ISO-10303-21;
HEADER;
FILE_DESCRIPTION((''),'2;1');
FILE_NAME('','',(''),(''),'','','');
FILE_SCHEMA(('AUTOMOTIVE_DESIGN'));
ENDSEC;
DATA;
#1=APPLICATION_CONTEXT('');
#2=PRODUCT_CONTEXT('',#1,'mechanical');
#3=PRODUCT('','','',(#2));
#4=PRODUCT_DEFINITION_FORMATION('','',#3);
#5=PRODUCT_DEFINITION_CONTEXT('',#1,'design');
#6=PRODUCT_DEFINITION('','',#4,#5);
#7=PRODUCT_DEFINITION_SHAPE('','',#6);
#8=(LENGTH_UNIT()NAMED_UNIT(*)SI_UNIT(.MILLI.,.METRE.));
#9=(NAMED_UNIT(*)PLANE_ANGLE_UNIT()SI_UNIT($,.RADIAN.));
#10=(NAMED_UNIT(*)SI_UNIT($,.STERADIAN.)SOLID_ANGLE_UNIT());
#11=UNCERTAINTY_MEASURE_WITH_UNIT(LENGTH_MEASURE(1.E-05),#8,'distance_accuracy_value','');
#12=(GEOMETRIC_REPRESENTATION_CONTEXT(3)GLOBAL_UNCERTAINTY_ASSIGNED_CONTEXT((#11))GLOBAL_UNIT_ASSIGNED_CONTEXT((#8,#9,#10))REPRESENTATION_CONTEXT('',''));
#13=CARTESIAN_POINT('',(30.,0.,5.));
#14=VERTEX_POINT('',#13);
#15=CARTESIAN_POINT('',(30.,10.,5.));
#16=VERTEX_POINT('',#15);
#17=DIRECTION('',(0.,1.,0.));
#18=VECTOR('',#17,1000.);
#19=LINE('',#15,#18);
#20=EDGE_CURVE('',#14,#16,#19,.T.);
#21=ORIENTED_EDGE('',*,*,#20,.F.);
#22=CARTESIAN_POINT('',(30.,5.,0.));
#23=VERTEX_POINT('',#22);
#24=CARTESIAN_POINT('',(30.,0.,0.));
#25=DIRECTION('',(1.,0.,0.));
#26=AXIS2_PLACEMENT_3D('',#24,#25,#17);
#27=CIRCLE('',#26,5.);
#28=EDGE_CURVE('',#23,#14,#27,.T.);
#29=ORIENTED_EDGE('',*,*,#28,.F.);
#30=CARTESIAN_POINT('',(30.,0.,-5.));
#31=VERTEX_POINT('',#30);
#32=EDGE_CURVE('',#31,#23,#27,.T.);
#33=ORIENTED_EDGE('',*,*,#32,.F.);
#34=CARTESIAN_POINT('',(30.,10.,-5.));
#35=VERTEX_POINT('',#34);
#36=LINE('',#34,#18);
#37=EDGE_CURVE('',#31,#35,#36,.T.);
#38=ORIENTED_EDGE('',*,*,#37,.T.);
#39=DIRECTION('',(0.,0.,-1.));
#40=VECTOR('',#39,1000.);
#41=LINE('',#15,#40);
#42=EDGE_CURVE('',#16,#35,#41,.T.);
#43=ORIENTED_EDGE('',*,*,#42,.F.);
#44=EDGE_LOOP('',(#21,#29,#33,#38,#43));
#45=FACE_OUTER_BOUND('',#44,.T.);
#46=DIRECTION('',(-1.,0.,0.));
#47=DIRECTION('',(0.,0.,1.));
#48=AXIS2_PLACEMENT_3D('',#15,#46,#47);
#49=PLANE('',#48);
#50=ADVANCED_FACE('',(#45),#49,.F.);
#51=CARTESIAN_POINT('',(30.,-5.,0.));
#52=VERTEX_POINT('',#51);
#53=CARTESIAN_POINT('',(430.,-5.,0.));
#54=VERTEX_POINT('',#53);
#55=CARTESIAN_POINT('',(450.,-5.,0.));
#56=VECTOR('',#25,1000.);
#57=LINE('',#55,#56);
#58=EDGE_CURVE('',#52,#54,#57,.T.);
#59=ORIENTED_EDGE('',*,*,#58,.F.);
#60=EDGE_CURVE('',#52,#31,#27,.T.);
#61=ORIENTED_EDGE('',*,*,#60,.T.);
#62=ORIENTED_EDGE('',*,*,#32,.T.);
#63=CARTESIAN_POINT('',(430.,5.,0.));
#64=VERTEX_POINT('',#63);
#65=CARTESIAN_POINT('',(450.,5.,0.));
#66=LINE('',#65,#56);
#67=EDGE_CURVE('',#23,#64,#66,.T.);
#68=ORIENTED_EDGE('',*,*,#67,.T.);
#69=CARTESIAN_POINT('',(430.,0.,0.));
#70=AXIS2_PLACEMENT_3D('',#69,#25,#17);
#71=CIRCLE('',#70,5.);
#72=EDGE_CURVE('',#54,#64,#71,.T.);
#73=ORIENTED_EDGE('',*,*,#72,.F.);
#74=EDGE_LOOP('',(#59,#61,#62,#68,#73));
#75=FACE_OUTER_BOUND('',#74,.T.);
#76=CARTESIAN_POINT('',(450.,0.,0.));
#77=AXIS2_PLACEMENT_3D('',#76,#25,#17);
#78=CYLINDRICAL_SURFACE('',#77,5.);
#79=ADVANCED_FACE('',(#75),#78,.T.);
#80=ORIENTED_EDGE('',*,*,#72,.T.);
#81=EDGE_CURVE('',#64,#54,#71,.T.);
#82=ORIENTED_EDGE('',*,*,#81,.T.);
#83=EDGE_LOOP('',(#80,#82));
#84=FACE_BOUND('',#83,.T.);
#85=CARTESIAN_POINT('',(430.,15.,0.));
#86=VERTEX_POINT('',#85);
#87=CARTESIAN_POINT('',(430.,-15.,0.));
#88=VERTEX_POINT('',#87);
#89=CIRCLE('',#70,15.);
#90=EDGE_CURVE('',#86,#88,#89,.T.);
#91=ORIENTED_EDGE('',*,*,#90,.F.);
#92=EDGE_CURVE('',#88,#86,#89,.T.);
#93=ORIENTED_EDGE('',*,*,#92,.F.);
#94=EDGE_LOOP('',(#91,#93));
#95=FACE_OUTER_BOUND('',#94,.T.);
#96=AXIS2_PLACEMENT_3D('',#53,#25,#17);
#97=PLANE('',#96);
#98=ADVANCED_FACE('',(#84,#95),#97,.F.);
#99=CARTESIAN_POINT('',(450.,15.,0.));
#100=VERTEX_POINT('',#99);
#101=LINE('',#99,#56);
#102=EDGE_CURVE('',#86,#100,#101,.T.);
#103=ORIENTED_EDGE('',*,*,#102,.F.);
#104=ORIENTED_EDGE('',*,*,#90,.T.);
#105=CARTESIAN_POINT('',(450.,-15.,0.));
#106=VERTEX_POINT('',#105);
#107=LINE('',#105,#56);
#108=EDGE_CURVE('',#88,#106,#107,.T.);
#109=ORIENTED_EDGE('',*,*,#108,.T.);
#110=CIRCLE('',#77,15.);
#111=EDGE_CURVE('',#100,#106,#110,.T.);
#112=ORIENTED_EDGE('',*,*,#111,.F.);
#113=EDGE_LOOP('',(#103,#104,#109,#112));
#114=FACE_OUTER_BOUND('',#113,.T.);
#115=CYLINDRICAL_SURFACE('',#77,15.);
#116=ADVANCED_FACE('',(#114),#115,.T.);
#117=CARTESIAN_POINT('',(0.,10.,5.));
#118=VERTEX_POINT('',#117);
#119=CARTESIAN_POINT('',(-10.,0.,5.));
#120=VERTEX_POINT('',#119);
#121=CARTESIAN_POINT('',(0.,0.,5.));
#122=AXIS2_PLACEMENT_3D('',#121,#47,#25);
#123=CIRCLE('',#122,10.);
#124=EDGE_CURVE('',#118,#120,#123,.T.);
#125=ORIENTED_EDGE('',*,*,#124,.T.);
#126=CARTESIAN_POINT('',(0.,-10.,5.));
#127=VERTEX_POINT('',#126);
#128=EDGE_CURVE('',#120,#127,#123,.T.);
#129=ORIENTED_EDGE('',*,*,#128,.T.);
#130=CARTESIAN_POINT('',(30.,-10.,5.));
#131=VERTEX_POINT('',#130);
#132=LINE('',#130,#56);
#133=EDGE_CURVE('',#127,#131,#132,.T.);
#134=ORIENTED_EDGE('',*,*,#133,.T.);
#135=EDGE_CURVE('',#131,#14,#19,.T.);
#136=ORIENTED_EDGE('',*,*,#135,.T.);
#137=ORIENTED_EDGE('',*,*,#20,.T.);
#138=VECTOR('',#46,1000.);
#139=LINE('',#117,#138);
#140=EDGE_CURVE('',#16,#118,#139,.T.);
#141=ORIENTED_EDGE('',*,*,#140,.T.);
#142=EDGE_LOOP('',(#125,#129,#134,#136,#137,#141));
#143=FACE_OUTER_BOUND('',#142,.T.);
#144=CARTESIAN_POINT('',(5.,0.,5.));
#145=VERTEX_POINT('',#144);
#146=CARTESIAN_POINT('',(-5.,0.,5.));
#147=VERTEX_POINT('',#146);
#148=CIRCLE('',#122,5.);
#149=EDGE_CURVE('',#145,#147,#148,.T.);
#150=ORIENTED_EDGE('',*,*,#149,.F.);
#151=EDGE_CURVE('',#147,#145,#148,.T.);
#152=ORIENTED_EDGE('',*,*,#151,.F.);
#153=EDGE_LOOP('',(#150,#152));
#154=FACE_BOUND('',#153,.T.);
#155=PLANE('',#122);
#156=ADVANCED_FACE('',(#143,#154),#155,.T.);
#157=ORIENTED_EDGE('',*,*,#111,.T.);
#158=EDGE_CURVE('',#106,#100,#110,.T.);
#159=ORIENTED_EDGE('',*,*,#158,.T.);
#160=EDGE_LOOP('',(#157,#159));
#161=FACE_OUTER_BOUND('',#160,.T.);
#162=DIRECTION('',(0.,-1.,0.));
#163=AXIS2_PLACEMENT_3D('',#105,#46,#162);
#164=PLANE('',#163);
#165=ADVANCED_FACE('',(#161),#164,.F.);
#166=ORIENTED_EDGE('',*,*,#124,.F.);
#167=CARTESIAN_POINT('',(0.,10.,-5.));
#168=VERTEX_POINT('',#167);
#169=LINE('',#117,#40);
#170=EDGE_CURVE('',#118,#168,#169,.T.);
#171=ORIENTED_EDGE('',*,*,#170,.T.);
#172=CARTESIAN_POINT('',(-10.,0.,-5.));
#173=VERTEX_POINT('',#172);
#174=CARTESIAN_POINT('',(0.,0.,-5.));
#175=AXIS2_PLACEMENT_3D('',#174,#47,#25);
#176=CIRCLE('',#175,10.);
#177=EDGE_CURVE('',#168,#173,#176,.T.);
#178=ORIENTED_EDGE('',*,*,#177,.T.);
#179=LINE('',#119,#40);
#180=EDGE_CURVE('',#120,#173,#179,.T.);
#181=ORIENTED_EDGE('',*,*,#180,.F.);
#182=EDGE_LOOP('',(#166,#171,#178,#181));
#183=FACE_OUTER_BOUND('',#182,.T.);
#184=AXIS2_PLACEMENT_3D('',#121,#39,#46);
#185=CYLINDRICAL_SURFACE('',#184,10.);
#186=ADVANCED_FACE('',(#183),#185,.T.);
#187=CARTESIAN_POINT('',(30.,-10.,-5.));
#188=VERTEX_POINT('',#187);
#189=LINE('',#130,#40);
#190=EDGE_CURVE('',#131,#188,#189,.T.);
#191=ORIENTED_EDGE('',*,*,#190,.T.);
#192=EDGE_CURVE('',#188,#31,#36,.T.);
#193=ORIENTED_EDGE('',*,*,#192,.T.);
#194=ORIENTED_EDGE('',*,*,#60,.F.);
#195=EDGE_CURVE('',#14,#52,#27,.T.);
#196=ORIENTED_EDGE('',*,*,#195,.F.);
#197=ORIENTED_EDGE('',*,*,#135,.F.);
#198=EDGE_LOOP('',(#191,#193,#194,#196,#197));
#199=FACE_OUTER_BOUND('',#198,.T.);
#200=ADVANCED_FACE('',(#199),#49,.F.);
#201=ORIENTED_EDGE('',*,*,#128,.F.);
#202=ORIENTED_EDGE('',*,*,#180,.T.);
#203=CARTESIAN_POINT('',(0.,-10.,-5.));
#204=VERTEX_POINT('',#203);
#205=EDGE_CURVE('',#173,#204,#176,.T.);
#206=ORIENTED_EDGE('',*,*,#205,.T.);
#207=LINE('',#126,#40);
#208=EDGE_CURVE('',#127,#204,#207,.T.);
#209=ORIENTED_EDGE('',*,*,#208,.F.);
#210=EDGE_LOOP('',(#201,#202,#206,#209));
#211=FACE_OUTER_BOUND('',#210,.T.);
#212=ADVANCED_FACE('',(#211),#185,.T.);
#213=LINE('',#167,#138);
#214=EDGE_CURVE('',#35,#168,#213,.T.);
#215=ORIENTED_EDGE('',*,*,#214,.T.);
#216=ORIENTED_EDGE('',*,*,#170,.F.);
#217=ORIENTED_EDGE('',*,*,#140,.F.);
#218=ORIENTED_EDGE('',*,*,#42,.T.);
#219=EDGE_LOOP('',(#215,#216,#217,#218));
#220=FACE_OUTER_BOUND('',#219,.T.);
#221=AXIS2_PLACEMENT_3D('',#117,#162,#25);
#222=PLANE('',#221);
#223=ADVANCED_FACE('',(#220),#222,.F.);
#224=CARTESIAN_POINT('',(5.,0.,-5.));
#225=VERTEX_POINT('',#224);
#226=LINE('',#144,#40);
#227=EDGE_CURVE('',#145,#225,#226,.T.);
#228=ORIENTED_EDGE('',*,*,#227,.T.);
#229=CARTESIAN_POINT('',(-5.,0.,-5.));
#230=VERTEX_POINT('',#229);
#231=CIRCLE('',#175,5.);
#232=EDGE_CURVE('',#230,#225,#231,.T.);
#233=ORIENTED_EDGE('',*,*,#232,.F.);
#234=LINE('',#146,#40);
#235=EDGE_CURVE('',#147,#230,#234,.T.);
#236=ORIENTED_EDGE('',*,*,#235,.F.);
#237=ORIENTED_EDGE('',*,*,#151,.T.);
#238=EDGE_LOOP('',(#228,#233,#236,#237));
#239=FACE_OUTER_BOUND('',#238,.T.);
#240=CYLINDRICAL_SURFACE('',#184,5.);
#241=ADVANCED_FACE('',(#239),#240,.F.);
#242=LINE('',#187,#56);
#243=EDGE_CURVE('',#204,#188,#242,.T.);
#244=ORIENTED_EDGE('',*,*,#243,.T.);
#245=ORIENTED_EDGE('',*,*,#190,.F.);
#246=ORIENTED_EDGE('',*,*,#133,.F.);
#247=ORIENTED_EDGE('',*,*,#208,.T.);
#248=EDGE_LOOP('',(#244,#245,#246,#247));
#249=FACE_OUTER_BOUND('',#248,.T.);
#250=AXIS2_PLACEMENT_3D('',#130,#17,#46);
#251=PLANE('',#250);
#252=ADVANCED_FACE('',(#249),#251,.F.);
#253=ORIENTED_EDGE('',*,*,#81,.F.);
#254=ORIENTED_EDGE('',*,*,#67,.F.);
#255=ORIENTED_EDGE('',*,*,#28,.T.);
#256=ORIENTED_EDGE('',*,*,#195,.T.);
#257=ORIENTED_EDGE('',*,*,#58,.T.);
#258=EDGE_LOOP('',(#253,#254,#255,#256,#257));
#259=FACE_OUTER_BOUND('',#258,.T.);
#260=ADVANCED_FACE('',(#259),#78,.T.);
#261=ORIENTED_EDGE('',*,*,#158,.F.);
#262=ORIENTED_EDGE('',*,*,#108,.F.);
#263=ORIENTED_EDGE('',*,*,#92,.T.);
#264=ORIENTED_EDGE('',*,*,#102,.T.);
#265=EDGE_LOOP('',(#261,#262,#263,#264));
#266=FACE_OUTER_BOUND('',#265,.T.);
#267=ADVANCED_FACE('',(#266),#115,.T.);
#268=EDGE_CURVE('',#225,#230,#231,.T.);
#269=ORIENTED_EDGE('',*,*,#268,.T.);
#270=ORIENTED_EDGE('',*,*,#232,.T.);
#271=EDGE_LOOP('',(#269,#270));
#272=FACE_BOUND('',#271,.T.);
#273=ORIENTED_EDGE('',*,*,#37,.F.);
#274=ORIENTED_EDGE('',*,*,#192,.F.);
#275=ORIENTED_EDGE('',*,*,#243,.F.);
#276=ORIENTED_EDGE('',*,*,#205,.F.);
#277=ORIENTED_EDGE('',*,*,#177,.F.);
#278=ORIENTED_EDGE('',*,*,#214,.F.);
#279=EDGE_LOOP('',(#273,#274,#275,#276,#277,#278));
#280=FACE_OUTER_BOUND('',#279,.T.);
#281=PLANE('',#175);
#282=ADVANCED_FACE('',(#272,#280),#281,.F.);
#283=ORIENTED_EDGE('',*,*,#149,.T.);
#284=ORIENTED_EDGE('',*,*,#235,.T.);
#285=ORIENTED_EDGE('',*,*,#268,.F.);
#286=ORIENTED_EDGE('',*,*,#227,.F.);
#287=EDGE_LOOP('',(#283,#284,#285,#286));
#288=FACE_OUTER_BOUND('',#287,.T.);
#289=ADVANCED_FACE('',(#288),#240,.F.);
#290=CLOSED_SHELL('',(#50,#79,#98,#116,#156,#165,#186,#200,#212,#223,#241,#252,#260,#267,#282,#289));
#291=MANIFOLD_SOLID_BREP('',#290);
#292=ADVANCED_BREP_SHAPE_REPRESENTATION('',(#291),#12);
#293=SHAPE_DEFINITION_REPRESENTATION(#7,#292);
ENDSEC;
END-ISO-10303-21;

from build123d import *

# Parameters (mm, degrees)
SKETCH1_R           = 5
BOSS_EXTRUDE1_DEPTH = 5


with BuildPart() as part:
    # Sketch1 → Boss-Extrude1 (new, symmetric)
    with BuildSketch(Plane.XY):
        with BuildLine():
            Line((0, 10), (30, 10))
            Line((30, 10), (30, -10))
            Line((30, -10), (0, -10))
            ThreePointArc((0, -10), (-10, 0), (0, 10))
        make_face()
        Circle(SKETCH1_R, mode=Mode.SUBTRACT)
    extrude(amount=BOSS_EXTRUDE1_DEPTH, both=True)

    # Sketch2 → Revolve1 (revolve)
    with BuildSketch(Plane.XY, mode=Mode.PRIVATE) as revolve1_sk:
        Polygon((30, 0), (30, -5), (430, -5), (430, -15), (450, -15), (450, 0), align=None)
    revolve(revolve1_sk.sketch.rotate(Axis((450, 0, 0), (-1, 0, 0)), 180), axis=Axis((450, 0, 0), (-1, 0, 0)))


solid = part.part
